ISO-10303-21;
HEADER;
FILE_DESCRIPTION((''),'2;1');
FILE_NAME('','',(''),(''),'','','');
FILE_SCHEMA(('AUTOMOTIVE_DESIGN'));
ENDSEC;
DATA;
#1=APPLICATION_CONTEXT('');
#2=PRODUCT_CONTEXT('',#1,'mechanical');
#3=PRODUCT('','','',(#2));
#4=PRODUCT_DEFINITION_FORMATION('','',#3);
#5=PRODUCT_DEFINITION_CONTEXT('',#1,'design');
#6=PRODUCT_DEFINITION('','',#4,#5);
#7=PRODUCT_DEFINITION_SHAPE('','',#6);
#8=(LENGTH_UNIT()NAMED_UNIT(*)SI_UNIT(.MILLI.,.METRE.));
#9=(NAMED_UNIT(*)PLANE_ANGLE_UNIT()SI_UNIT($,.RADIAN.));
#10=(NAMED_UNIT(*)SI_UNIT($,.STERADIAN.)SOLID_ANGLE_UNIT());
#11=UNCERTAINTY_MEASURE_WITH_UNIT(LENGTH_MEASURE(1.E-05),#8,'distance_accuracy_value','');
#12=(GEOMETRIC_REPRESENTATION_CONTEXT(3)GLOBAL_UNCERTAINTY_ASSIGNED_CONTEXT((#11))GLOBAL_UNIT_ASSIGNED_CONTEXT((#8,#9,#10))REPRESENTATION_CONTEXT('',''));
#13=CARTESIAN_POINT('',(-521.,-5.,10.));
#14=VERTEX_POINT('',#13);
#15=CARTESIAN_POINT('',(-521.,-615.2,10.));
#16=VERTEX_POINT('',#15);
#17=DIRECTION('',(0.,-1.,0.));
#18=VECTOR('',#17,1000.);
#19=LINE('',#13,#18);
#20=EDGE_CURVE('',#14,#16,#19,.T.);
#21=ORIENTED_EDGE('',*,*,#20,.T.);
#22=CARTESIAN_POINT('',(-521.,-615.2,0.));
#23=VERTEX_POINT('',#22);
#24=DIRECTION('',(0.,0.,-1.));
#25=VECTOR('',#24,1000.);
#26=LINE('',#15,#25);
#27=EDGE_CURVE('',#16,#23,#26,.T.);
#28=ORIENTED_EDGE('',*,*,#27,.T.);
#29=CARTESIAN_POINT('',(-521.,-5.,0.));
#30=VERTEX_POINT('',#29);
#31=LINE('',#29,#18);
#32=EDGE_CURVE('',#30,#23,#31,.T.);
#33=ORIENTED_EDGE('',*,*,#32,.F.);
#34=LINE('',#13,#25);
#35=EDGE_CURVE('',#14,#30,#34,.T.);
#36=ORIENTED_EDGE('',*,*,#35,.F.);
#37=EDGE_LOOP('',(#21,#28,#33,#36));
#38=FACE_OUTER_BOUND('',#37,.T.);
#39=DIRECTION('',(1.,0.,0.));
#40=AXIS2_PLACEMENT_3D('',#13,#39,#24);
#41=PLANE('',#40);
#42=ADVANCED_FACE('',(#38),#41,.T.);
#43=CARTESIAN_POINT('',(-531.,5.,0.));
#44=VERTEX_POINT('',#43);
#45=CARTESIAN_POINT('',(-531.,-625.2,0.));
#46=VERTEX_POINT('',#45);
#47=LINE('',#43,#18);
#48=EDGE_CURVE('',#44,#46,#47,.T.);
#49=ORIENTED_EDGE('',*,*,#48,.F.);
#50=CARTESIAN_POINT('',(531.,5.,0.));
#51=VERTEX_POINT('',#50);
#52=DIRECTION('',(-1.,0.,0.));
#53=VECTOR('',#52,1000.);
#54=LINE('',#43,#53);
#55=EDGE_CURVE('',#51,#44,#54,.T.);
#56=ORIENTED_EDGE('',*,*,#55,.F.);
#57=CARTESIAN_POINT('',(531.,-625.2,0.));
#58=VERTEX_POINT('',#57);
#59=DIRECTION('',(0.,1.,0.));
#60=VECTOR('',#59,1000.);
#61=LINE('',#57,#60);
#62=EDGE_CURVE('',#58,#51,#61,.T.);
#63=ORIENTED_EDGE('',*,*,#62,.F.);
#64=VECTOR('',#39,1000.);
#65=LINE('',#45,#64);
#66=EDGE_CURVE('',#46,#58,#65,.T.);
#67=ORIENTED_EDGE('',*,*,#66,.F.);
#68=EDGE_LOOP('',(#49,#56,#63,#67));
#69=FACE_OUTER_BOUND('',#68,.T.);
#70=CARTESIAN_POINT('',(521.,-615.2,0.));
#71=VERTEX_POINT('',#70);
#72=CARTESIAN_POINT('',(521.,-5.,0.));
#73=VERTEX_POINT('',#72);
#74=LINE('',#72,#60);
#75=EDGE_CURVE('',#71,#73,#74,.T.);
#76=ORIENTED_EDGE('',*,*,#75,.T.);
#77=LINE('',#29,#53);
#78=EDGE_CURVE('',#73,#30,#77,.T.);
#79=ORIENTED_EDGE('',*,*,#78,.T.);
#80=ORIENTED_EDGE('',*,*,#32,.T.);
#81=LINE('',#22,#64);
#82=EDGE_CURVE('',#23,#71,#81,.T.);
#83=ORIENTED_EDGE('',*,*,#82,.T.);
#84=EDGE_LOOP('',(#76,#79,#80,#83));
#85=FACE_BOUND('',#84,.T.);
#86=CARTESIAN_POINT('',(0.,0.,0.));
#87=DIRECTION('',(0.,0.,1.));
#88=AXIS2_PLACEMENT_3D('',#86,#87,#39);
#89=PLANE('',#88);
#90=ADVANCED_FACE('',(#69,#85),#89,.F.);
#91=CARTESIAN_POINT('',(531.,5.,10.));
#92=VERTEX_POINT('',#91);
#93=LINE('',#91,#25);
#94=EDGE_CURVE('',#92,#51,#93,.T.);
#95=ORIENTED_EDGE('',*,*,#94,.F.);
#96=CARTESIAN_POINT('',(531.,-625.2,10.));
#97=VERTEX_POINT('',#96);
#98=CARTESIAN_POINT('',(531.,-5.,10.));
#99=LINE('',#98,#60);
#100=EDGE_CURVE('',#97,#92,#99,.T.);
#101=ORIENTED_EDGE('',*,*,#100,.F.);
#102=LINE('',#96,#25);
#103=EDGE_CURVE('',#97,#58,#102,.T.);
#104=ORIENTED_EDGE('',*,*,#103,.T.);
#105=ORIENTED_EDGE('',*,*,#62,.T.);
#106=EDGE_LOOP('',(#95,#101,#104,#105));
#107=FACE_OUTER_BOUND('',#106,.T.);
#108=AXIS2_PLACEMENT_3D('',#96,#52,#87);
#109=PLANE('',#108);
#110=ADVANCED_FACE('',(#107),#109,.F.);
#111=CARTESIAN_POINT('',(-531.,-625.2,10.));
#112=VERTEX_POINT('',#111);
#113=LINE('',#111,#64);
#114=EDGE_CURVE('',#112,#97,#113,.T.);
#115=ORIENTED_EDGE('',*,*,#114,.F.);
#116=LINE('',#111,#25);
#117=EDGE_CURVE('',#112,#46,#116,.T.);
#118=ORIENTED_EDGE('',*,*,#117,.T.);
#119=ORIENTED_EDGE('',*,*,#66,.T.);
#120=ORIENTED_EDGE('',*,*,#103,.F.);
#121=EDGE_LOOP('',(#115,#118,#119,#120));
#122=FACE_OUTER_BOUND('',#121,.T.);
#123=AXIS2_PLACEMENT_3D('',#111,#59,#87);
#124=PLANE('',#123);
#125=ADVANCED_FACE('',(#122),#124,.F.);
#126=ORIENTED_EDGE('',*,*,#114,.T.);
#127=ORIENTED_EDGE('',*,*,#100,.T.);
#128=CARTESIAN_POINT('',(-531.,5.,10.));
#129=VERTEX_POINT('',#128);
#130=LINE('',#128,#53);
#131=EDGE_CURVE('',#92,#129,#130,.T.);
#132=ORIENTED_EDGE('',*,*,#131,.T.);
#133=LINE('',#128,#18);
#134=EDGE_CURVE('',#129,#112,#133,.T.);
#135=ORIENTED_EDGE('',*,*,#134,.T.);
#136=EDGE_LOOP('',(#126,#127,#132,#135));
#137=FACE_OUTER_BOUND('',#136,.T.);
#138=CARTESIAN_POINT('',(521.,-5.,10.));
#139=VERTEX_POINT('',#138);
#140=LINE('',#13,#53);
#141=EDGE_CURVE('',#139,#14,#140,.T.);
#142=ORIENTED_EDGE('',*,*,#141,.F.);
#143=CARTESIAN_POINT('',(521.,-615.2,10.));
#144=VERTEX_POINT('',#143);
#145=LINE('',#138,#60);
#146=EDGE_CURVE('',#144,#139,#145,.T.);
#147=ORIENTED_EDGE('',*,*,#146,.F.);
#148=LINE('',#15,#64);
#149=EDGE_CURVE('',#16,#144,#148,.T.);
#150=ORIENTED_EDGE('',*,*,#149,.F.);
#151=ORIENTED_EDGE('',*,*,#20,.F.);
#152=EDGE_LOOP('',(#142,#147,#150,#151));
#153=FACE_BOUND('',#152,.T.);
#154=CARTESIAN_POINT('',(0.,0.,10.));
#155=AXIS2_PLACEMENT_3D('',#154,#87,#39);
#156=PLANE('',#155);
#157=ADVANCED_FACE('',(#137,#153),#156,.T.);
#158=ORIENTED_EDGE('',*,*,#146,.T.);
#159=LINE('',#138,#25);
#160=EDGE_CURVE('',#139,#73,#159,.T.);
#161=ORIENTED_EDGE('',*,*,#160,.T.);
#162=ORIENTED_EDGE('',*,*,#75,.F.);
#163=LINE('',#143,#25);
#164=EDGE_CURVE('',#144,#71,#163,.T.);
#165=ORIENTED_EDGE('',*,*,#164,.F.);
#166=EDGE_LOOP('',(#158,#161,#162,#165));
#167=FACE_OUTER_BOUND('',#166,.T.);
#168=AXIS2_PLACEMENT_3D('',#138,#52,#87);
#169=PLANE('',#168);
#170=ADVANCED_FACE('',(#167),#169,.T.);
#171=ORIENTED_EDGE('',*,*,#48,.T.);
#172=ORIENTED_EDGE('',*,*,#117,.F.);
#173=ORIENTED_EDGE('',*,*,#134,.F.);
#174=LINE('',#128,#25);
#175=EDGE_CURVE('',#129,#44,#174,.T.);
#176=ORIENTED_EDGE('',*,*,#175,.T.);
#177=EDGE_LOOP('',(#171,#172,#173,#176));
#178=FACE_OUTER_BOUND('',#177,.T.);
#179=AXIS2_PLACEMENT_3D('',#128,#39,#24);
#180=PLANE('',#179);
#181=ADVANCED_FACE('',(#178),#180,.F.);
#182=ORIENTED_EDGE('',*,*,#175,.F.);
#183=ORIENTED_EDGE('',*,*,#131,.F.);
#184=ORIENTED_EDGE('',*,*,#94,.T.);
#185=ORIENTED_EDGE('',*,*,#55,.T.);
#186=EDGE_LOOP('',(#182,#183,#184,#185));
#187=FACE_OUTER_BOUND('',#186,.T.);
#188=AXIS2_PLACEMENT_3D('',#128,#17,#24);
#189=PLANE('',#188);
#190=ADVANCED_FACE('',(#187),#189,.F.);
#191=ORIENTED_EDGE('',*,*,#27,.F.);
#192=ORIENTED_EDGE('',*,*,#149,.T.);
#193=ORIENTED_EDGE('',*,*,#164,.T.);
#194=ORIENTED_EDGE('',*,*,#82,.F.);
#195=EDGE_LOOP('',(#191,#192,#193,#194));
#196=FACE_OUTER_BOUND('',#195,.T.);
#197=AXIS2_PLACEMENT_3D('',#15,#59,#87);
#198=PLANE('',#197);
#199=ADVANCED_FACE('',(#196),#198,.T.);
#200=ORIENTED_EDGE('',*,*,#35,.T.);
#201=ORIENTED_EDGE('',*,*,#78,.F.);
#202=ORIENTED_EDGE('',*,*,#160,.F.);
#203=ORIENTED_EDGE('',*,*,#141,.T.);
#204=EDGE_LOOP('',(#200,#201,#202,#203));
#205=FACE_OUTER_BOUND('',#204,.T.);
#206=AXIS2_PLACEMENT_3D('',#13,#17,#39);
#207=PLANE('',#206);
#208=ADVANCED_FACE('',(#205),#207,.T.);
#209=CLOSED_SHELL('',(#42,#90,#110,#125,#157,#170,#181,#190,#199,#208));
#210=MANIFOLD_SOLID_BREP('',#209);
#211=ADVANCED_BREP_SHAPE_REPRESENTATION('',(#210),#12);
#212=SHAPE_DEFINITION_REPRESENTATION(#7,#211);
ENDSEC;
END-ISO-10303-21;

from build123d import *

# Parameters (mm, degrees)
SKETCH_1_W      = 1042
SKETCH_1_H      = 610.2
EXTRUDE_1_DEPTH = 10


with BuildPart() as part:
    # 草图1 → 凸台-拉伸1 (new body)
    with BuildSketch(Plane.XY):
        Polygon((-531, 5), (531, 5), (531, -5), (531, -615.2), (531, -625.2), (-531, -625.2), align=None)
        with Locations((0, -310.1)):
            Rectangle(SKETCH_1_W, SKETCH_1_H, mode=Mode.SUBTRACT)
    extrude(amount=EXTRUDE_1_DEPTH)


solid = part.part
